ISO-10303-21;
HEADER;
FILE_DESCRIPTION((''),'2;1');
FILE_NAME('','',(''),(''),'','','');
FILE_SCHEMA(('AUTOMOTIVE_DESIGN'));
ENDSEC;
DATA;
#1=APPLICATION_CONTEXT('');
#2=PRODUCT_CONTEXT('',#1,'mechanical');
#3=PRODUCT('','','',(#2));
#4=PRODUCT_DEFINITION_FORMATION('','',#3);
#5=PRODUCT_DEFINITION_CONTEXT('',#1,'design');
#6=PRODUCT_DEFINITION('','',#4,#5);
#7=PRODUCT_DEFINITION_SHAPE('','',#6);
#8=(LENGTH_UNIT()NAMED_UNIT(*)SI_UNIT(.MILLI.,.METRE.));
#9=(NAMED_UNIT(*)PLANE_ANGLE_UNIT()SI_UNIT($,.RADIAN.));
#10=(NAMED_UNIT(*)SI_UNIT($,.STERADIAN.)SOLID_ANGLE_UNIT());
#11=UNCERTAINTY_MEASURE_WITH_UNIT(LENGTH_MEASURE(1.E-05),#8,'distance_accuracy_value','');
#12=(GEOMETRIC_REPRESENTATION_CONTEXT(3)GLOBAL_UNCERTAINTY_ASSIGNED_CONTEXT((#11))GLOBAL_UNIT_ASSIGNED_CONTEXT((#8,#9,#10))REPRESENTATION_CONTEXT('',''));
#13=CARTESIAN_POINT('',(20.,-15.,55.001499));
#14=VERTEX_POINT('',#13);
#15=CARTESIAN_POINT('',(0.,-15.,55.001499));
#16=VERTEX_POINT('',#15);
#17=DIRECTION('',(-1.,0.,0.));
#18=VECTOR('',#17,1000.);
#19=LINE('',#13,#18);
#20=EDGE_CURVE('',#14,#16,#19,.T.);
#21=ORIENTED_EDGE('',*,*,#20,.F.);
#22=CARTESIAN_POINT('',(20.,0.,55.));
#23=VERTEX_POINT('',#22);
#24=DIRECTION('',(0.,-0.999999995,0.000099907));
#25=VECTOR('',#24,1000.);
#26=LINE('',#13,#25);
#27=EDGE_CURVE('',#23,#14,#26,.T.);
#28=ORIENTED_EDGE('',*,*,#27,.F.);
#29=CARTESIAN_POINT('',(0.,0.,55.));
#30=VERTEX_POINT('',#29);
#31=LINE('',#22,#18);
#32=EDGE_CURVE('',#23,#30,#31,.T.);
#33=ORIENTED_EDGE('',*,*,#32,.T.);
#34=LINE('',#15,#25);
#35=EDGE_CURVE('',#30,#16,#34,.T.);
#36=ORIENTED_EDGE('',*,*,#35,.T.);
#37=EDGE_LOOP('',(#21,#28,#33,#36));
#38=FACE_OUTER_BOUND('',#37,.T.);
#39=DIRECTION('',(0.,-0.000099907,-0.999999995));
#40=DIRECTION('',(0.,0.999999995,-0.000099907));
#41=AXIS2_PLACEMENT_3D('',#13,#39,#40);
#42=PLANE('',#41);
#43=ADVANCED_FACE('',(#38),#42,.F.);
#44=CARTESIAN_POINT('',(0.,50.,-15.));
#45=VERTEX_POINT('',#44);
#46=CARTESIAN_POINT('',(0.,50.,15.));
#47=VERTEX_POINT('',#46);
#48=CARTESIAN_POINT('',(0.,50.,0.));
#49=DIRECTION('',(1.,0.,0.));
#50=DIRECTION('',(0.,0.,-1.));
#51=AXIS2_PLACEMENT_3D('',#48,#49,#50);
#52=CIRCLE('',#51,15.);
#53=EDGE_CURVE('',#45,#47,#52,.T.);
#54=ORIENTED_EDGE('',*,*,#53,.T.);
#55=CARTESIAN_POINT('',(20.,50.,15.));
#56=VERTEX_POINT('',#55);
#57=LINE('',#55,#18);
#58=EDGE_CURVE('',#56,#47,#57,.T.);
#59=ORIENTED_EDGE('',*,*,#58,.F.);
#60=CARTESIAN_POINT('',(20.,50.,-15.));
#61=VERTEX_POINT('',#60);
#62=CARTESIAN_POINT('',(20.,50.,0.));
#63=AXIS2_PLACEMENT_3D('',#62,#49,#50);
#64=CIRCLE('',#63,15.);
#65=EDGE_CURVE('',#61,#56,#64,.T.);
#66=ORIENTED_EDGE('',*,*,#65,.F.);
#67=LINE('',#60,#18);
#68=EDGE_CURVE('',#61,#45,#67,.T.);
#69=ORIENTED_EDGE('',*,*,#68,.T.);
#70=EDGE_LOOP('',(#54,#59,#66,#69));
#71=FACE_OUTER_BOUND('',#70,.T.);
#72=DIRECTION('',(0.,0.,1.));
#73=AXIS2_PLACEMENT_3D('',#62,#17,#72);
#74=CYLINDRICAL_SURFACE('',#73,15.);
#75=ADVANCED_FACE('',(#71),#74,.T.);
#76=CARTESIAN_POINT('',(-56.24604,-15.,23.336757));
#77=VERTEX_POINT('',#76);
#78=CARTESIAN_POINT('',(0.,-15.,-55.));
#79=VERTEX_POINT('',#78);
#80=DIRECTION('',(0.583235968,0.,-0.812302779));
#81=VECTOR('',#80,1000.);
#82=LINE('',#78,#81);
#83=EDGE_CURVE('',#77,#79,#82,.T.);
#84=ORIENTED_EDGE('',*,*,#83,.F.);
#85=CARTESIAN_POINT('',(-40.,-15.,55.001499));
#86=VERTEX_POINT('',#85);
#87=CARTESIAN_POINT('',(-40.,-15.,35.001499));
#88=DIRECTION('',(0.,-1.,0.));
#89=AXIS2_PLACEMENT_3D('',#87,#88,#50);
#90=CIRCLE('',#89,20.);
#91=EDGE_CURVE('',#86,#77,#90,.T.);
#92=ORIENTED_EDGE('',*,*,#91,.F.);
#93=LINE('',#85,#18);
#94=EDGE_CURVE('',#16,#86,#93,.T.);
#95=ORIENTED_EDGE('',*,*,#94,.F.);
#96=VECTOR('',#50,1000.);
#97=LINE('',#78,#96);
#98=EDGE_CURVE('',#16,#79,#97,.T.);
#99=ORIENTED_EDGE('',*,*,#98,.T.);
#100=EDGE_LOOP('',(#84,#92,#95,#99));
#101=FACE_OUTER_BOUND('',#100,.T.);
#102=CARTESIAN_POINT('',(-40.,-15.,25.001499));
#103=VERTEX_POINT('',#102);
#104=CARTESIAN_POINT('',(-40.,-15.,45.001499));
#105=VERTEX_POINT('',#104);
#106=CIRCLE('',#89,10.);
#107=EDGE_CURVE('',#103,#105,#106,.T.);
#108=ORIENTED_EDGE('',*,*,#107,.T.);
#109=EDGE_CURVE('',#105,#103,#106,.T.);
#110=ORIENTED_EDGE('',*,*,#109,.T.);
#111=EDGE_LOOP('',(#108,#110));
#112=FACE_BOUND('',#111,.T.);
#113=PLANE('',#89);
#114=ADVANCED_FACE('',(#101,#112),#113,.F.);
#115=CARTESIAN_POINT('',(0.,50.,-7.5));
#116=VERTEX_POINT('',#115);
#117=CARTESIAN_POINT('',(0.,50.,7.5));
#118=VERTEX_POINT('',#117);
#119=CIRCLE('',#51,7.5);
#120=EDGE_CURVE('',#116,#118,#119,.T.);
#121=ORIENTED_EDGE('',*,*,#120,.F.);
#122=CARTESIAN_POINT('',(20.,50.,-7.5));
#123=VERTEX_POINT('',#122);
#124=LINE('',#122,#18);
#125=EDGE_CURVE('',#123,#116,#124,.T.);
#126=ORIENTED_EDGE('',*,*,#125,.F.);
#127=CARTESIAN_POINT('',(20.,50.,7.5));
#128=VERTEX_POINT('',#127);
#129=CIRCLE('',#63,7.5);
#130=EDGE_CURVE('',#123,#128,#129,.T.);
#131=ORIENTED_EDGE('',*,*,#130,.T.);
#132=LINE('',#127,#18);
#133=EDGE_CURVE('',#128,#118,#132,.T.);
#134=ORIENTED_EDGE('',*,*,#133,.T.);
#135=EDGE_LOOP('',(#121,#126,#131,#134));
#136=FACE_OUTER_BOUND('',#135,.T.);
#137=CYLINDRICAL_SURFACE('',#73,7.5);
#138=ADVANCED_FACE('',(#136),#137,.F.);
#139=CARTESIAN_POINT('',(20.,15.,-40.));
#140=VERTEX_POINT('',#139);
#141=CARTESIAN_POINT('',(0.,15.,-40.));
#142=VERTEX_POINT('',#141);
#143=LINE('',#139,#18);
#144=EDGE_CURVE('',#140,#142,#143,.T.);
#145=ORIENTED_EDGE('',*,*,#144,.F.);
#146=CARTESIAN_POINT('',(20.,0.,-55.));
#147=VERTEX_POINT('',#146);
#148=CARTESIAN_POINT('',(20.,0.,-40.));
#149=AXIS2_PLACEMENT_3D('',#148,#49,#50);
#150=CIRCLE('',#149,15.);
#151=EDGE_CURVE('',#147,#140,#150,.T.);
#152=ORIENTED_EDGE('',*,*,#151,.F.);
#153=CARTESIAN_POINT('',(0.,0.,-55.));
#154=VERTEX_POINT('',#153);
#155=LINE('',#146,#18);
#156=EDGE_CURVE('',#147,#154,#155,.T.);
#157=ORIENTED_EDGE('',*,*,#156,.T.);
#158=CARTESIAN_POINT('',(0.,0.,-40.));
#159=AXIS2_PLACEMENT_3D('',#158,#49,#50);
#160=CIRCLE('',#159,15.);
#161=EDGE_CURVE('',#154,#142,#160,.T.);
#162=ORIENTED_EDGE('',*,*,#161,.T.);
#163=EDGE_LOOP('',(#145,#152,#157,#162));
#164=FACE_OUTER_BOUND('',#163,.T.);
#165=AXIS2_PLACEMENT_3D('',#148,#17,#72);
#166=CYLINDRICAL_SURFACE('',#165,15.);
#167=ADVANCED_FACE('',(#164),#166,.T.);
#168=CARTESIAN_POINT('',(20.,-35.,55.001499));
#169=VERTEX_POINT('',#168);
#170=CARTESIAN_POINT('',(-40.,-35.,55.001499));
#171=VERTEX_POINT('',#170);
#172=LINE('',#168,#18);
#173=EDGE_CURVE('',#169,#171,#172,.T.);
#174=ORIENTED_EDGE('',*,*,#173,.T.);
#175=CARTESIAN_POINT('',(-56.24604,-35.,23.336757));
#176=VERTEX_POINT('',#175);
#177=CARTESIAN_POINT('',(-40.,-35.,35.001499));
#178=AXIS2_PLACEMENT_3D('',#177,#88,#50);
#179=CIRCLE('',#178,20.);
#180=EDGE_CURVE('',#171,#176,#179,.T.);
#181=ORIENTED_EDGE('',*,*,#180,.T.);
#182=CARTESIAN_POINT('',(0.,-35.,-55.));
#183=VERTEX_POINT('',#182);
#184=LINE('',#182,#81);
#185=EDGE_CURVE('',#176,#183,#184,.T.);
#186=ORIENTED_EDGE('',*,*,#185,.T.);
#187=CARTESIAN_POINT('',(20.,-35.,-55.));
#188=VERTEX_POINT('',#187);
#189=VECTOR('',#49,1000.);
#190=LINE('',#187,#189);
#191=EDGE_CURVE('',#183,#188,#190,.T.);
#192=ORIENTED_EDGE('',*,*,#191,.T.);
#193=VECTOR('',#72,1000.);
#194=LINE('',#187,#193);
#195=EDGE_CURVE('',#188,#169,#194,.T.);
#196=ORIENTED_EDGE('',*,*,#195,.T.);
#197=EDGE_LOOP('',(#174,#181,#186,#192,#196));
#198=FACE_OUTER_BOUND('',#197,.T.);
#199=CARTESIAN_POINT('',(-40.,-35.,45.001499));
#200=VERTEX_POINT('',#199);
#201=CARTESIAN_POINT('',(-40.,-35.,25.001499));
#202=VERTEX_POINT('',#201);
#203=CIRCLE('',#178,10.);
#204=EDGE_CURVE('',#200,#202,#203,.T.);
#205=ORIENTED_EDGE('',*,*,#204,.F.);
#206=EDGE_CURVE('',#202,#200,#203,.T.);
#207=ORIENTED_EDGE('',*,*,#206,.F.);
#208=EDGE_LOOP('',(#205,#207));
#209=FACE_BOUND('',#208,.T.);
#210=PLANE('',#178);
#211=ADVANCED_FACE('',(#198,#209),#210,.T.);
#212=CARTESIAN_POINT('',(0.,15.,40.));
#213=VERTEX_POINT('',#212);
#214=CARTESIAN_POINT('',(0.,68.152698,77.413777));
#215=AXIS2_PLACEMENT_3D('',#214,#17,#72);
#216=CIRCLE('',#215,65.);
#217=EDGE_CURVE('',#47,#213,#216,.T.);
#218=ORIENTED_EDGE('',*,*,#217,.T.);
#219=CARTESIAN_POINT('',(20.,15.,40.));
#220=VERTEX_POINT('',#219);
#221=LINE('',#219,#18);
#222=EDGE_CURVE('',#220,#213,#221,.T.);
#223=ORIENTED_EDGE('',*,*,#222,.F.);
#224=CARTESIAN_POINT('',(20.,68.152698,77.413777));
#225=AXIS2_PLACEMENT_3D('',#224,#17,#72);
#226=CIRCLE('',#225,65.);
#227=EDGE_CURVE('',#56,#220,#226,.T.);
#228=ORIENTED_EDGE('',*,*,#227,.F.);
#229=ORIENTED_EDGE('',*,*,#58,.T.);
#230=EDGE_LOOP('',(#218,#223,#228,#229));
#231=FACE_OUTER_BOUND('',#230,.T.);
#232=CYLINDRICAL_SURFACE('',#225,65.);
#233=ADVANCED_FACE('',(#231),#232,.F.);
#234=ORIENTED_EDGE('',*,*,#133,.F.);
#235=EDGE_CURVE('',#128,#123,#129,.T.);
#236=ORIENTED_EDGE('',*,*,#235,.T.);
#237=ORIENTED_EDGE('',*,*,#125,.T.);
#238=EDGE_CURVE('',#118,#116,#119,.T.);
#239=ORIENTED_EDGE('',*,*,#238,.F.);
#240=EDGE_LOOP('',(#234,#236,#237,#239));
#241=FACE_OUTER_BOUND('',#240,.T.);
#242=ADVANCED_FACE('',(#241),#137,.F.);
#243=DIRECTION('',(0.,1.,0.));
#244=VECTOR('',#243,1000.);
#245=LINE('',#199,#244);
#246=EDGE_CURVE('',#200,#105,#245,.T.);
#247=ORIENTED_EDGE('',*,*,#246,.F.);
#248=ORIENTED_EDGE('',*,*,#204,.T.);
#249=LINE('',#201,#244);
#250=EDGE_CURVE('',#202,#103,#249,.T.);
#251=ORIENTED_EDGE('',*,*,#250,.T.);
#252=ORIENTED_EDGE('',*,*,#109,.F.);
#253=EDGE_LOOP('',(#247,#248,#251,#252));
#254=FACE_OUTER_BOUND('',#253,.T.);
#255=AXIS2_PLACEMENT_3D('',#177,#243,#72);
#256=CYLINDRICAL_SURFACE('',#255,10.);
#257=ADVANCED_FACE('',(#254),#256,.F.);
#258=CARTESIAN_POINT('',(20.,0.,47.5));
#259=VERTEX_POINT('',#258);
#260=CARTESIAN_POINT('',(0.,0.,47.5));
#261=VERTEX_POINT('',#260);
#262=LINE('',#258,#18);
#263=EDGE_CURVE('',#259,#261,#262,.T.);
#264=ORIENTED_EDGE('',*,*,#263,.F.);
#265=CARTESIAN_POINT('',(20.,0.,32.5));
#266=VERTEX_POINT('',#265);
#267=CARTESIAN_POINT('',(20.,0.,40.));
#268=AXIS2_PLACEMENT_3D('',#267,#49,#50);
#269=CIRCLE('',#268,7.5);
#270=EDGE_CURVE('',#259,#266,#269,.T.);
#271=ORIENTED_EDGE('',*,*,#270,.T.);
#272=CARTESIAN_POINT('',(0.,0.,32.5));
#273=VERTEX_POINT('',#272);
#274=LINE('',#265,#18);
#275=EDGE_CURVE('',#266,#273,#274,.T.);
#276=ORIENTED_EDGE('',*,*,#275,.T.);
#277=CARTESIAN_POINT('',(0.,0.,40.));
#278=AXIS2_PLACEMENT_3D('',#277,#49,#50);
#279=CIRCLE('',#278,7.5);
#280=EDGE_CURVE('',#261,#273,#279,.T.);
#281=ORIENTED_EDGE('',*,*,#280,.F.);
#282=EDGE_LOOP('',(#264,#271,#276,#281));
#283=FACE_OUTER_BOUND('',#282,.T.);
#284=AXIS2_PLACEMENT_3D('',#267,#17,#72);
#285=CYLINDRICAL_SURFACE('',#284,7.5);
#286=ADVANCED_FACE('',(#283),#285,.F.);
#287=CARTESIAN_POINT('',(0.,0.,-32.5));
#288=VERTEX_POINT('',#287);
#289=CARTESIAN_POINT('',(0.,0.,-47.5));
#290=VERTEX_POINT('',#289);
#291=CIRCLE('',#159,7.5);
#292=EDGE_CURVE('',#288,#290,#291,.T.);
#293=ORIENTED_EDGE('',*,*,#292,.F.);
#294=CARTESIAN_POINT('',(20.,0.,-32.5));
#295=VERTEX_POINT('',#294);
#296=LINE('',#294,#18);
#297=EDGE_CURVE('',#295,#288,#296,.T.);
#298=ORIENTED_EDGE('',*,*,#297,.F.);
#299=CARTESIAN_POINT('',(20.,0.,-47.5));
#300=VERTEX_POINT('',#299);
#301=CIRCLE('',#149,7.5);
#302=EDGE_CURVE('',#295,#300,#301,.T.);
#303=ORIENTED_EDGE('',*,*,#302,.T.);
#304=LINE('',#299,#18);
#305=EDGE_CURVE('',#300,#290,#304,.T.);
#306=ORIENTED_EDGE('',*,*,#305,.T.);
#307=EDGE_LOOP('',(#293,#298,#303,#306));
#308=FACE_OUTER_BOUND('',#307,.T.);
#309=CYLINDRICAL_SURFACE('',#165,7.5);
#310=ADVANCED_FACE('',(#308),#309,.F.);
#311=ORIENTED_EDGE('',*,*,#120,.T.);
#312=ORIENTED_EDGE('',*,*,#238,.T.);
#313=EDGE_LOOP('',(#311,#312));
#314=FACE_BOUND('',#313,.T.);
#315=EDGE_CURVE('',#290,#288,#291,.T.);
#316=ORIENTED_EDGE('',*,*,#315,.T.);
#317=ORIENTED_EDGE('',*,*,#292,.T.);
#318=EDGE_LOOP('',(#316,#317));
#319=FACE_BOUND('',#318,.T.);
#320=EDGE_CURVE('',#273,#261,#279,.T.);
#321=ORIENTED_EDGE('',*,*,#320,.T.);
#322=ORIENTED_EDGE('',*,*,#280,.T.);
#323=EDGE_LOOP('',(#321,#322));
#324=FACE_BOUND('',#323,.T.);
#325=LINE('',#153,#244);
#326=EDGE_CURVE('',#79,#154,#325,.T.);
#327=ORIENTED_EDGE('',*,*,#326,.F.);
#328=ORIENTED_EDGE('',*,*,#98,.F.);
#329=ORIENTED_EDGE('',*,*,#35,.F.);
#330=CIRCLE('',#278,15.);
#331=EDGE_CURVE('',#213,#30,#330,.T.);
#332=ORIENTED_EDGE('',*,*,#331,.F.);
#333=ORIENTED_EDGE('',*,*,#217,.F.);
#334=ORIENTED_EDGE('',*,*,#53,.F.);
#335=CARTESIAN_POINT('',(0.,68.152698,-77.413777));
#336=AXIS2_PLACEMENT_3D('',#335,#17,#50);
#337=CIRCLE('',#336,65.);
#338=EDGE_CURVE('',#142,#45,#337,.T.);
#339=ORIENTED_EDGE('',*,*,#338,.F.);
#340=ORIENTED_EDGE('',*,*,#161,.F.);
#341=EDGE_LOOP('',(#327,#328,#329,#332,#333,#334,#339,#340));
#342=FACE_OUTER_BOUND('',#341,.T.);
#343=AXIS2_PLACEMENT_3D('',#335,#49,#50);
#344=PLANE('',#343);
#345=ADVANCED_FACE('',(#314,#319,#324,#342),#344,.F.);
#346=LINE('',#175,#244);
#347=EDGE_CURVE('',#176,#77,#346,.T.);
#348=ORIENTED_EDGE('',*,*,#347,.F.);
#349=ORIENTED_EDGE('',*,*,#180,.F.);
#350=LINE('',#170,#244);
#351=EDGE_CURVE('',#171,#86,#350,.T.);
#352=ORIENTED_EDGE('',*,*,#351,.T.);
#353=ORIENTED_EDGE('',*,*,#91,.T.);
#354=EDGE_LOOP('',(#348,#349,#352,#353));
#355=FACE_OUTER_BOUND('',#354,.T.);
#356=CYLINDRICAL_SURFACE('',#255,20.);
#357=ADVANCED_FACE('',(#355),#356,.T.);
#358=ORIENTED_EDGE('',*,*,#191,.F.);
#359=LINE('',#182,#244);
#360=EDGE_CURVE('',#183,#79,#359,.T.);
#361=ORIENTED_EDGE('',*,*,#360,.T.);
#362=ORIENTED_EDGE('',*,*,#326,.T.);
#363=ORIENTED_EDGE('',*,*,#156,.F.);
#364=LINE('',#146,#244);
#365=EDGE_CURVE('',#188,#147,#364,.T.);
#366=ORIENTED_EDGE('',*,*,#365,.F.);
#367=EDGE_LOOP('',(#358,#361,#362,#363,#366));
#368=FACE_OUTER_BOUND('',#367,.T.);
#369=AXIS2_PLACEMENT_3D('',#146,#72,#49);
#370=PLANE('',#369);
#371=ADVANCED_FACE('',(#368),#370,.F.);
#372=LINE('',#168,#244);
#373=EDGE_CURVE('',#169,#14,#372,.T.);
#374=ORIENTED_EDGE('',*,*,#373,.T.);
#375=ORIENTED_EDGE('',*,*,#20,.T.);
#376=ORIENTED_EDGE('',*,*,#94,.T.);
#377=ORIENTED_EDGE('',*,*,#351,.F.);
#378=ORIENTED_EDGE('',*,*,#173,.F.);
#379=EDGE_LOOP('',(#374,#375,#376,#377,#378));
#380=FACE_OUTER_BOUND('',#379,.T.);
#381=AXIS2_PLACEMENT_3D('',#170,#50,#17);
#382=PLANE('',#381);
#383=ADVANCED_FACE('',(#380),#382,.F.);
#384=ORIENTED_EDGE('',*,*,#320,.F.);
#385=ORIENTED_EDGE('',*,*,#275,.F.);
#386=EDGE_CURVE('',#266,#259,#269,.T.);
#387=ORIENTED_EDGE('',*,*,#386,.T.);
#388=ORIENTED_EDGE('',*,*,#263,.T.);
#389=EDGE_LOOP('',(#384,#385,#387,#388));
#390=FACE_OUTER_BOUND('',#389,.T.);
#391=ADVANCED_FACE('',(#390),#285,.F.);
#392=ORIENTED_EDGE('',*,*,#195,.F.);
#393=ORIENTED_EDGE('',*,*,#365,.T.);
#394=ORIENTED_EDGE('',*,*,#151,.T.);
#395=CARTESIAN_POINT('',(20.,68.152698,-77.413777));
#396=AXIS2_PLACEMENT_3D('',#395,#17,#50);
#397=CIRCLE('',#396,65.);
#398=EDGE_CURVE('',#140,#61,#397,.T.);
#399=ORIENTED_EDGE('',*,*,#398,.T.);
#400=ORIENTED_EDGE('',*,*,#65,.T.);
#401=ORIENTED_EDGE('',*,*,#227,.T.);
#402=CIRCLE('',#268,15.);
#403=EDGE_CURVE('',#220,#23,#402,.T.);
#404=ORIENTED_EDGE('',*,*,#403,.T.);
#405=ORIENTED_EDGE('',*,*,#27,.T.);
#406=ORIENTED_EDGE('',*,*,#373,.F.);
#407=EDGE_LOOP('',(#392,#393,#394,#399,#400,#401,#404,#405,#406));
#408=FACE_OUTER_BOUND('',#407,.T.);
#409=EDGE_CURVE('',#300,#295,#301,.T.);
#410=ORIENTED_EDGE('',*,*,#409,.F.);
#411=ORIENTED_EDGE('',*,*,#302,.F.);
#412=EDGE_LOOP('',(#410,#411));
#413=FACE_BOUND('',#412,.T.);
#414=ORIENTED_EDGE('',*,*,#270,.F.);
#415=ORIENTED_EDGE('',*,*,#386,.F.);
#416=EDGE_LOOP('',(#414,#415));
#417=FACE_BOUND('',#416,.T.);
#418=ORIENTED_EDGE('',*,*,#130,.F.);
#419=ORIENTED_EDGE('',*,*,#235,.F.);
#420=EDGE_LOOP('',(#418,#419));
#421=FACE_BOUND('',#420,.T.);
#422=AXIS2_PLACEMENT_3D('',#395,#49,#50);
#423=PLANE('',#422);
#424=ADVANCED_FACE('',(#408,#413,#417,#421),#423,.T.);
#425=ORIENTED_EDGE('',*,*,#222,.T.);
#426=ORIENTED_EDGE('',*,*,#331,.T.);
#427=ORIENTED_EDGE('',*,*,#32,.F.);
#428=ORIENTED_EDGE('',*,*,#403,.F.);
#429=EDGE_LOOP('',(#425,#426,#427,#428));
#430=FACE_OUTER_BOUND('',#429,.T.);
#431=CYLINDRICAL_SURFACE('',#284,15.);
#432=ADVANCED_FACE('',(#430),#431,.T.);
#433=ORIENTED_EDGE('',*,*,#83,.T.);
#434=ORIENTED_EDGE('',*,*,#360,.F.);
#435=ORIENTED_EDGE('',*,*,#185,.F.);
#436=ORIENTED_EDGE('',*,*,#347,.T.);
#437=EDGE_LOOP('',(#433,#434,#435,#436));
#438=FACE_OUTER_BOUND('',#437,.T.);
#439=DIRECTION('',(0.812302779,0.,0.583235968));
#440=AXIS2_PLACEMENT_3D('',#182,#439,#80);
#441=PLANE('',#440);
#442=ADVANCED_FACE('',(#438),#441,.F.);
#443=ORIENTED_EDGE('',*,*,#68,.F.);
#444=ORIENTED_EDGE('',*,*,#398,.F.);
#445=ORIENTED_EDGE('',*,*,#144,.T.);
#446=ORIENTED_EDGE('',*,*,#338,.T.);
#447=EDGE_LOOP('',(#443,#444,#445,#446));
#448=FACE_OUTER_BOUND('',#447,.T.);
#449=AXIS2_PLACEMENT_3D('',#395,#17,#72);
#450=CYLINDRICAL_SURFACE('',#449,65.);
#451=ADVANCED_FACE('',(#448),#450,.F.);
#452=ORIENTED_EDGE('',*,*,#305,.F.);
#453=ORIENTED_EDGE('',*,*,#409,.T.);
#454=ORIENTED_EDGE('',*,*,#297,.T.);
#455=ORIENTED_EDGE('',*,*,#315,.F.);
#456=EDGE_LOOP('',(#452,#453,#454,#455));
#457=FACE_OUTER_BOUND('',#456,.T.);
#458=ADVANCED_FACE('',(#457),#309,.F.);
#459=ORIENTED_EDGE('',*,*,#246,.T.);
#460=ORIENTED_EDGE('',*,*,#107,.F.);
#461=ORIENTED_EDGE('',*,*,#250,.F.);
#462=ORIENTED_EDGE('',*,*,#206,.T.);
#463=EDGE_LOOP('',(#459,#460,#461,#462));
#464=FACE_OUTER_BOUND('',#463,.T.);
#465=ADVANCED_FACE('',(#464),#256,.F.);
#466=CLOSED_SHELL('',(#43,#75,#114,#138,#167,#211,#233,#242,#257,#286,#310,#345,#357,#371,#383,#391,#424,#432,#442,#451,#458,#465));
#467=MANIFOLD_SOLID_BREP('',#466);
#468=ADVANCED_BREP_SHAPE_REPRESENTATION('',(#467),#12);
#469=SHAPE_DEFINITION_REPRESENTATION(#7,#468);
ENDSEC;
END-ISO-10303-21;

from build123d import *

# Parameters (mm, degrees)
BRACKET_PROFILE_SKETCH_R   = 7.5
BRACKET_PROFILE_BOSS_DEPTH = 20
BASE_BLOCK_SKETCH_R        = 10
BASE_BLOCK_BOSS_DEPTH      = 20


with BuildPart() as part:
    # Bracket Profile Sketch → Bracket Profile Boss (new body)
    with BuildSketch(Plane(origin=(0, 0, 0), x_dir=(0, 0, -1), z_dir=(1, 0, 0))):
        with BuildLine():
            Line((55, 0), (55, -15))
            Line((55, -15), (-55.001498604, -15))
            Line((-55.001498604, -15), (-55, 0))
            ThreePointArc((-55, 0), (-50.606601718, 10.606601718), (-40, 15))
            ThreePointArc((-40, 15), (-24.521101379, 30.372215271), (-15, 50))
            ThreePointArc((-15, 50), (0, 65), (15, 50))
            ThreePointArc((15, 50), (24.521101379, 30.372215271), (40, 15))
            ThreePointArc((40, 15), (50.606601718, 10.606601718), (55, 0))
        make_face()
        with Locations((0, 50)):
            Circle(BRACKET_PROFILE_SKETCH_R, mode=Mode.SUBTRACT)
        with Locations((40, 0)):
            Circle(BRACKET_PROFILE_SKETCH_R, mode=Mode.SUBTRACT)
        with Locations((-40, 0)):
            Circle(BRACKET_PROFILE_SKETCH_R, mode=Mode.SUBTRACT)
    extrude(amount=BRACKET_PROFILE_BOSS_DEPTH)

    # Base Block Sketch → Base Block Boss (add)
    with BuildSketch(Plane(origin=(0, -15, 0), x_dir=(-1, 0, 0), z_dir=(0, -1, 0))):
        with BuildLine():
            Line((-20, 55), (-20, -55.001498604))
            Line((-20, -55.001498604), (0, -55.001498604))
            Line((0, -55.001498604), (40, -55.001498604))
            ThreePointArc((40, -55.001498604), (57.794589541, -44.131262187), (56.246039556, -23.336756912))
            Line((56.246039556, -23.336756912), (0, 55))
            Line((0, 55), (-20, 55))
        make_face()
        with Locations(Location((40, -35.001498604, 0), (0, 0, 90))):
            Circle(BASE_BLOCK_SKETCH_R, mode=Mode.SUBTRACT)
    extrude(amount=BASE_BLOCK_BOSS_DEPTH)


solid = part.part
